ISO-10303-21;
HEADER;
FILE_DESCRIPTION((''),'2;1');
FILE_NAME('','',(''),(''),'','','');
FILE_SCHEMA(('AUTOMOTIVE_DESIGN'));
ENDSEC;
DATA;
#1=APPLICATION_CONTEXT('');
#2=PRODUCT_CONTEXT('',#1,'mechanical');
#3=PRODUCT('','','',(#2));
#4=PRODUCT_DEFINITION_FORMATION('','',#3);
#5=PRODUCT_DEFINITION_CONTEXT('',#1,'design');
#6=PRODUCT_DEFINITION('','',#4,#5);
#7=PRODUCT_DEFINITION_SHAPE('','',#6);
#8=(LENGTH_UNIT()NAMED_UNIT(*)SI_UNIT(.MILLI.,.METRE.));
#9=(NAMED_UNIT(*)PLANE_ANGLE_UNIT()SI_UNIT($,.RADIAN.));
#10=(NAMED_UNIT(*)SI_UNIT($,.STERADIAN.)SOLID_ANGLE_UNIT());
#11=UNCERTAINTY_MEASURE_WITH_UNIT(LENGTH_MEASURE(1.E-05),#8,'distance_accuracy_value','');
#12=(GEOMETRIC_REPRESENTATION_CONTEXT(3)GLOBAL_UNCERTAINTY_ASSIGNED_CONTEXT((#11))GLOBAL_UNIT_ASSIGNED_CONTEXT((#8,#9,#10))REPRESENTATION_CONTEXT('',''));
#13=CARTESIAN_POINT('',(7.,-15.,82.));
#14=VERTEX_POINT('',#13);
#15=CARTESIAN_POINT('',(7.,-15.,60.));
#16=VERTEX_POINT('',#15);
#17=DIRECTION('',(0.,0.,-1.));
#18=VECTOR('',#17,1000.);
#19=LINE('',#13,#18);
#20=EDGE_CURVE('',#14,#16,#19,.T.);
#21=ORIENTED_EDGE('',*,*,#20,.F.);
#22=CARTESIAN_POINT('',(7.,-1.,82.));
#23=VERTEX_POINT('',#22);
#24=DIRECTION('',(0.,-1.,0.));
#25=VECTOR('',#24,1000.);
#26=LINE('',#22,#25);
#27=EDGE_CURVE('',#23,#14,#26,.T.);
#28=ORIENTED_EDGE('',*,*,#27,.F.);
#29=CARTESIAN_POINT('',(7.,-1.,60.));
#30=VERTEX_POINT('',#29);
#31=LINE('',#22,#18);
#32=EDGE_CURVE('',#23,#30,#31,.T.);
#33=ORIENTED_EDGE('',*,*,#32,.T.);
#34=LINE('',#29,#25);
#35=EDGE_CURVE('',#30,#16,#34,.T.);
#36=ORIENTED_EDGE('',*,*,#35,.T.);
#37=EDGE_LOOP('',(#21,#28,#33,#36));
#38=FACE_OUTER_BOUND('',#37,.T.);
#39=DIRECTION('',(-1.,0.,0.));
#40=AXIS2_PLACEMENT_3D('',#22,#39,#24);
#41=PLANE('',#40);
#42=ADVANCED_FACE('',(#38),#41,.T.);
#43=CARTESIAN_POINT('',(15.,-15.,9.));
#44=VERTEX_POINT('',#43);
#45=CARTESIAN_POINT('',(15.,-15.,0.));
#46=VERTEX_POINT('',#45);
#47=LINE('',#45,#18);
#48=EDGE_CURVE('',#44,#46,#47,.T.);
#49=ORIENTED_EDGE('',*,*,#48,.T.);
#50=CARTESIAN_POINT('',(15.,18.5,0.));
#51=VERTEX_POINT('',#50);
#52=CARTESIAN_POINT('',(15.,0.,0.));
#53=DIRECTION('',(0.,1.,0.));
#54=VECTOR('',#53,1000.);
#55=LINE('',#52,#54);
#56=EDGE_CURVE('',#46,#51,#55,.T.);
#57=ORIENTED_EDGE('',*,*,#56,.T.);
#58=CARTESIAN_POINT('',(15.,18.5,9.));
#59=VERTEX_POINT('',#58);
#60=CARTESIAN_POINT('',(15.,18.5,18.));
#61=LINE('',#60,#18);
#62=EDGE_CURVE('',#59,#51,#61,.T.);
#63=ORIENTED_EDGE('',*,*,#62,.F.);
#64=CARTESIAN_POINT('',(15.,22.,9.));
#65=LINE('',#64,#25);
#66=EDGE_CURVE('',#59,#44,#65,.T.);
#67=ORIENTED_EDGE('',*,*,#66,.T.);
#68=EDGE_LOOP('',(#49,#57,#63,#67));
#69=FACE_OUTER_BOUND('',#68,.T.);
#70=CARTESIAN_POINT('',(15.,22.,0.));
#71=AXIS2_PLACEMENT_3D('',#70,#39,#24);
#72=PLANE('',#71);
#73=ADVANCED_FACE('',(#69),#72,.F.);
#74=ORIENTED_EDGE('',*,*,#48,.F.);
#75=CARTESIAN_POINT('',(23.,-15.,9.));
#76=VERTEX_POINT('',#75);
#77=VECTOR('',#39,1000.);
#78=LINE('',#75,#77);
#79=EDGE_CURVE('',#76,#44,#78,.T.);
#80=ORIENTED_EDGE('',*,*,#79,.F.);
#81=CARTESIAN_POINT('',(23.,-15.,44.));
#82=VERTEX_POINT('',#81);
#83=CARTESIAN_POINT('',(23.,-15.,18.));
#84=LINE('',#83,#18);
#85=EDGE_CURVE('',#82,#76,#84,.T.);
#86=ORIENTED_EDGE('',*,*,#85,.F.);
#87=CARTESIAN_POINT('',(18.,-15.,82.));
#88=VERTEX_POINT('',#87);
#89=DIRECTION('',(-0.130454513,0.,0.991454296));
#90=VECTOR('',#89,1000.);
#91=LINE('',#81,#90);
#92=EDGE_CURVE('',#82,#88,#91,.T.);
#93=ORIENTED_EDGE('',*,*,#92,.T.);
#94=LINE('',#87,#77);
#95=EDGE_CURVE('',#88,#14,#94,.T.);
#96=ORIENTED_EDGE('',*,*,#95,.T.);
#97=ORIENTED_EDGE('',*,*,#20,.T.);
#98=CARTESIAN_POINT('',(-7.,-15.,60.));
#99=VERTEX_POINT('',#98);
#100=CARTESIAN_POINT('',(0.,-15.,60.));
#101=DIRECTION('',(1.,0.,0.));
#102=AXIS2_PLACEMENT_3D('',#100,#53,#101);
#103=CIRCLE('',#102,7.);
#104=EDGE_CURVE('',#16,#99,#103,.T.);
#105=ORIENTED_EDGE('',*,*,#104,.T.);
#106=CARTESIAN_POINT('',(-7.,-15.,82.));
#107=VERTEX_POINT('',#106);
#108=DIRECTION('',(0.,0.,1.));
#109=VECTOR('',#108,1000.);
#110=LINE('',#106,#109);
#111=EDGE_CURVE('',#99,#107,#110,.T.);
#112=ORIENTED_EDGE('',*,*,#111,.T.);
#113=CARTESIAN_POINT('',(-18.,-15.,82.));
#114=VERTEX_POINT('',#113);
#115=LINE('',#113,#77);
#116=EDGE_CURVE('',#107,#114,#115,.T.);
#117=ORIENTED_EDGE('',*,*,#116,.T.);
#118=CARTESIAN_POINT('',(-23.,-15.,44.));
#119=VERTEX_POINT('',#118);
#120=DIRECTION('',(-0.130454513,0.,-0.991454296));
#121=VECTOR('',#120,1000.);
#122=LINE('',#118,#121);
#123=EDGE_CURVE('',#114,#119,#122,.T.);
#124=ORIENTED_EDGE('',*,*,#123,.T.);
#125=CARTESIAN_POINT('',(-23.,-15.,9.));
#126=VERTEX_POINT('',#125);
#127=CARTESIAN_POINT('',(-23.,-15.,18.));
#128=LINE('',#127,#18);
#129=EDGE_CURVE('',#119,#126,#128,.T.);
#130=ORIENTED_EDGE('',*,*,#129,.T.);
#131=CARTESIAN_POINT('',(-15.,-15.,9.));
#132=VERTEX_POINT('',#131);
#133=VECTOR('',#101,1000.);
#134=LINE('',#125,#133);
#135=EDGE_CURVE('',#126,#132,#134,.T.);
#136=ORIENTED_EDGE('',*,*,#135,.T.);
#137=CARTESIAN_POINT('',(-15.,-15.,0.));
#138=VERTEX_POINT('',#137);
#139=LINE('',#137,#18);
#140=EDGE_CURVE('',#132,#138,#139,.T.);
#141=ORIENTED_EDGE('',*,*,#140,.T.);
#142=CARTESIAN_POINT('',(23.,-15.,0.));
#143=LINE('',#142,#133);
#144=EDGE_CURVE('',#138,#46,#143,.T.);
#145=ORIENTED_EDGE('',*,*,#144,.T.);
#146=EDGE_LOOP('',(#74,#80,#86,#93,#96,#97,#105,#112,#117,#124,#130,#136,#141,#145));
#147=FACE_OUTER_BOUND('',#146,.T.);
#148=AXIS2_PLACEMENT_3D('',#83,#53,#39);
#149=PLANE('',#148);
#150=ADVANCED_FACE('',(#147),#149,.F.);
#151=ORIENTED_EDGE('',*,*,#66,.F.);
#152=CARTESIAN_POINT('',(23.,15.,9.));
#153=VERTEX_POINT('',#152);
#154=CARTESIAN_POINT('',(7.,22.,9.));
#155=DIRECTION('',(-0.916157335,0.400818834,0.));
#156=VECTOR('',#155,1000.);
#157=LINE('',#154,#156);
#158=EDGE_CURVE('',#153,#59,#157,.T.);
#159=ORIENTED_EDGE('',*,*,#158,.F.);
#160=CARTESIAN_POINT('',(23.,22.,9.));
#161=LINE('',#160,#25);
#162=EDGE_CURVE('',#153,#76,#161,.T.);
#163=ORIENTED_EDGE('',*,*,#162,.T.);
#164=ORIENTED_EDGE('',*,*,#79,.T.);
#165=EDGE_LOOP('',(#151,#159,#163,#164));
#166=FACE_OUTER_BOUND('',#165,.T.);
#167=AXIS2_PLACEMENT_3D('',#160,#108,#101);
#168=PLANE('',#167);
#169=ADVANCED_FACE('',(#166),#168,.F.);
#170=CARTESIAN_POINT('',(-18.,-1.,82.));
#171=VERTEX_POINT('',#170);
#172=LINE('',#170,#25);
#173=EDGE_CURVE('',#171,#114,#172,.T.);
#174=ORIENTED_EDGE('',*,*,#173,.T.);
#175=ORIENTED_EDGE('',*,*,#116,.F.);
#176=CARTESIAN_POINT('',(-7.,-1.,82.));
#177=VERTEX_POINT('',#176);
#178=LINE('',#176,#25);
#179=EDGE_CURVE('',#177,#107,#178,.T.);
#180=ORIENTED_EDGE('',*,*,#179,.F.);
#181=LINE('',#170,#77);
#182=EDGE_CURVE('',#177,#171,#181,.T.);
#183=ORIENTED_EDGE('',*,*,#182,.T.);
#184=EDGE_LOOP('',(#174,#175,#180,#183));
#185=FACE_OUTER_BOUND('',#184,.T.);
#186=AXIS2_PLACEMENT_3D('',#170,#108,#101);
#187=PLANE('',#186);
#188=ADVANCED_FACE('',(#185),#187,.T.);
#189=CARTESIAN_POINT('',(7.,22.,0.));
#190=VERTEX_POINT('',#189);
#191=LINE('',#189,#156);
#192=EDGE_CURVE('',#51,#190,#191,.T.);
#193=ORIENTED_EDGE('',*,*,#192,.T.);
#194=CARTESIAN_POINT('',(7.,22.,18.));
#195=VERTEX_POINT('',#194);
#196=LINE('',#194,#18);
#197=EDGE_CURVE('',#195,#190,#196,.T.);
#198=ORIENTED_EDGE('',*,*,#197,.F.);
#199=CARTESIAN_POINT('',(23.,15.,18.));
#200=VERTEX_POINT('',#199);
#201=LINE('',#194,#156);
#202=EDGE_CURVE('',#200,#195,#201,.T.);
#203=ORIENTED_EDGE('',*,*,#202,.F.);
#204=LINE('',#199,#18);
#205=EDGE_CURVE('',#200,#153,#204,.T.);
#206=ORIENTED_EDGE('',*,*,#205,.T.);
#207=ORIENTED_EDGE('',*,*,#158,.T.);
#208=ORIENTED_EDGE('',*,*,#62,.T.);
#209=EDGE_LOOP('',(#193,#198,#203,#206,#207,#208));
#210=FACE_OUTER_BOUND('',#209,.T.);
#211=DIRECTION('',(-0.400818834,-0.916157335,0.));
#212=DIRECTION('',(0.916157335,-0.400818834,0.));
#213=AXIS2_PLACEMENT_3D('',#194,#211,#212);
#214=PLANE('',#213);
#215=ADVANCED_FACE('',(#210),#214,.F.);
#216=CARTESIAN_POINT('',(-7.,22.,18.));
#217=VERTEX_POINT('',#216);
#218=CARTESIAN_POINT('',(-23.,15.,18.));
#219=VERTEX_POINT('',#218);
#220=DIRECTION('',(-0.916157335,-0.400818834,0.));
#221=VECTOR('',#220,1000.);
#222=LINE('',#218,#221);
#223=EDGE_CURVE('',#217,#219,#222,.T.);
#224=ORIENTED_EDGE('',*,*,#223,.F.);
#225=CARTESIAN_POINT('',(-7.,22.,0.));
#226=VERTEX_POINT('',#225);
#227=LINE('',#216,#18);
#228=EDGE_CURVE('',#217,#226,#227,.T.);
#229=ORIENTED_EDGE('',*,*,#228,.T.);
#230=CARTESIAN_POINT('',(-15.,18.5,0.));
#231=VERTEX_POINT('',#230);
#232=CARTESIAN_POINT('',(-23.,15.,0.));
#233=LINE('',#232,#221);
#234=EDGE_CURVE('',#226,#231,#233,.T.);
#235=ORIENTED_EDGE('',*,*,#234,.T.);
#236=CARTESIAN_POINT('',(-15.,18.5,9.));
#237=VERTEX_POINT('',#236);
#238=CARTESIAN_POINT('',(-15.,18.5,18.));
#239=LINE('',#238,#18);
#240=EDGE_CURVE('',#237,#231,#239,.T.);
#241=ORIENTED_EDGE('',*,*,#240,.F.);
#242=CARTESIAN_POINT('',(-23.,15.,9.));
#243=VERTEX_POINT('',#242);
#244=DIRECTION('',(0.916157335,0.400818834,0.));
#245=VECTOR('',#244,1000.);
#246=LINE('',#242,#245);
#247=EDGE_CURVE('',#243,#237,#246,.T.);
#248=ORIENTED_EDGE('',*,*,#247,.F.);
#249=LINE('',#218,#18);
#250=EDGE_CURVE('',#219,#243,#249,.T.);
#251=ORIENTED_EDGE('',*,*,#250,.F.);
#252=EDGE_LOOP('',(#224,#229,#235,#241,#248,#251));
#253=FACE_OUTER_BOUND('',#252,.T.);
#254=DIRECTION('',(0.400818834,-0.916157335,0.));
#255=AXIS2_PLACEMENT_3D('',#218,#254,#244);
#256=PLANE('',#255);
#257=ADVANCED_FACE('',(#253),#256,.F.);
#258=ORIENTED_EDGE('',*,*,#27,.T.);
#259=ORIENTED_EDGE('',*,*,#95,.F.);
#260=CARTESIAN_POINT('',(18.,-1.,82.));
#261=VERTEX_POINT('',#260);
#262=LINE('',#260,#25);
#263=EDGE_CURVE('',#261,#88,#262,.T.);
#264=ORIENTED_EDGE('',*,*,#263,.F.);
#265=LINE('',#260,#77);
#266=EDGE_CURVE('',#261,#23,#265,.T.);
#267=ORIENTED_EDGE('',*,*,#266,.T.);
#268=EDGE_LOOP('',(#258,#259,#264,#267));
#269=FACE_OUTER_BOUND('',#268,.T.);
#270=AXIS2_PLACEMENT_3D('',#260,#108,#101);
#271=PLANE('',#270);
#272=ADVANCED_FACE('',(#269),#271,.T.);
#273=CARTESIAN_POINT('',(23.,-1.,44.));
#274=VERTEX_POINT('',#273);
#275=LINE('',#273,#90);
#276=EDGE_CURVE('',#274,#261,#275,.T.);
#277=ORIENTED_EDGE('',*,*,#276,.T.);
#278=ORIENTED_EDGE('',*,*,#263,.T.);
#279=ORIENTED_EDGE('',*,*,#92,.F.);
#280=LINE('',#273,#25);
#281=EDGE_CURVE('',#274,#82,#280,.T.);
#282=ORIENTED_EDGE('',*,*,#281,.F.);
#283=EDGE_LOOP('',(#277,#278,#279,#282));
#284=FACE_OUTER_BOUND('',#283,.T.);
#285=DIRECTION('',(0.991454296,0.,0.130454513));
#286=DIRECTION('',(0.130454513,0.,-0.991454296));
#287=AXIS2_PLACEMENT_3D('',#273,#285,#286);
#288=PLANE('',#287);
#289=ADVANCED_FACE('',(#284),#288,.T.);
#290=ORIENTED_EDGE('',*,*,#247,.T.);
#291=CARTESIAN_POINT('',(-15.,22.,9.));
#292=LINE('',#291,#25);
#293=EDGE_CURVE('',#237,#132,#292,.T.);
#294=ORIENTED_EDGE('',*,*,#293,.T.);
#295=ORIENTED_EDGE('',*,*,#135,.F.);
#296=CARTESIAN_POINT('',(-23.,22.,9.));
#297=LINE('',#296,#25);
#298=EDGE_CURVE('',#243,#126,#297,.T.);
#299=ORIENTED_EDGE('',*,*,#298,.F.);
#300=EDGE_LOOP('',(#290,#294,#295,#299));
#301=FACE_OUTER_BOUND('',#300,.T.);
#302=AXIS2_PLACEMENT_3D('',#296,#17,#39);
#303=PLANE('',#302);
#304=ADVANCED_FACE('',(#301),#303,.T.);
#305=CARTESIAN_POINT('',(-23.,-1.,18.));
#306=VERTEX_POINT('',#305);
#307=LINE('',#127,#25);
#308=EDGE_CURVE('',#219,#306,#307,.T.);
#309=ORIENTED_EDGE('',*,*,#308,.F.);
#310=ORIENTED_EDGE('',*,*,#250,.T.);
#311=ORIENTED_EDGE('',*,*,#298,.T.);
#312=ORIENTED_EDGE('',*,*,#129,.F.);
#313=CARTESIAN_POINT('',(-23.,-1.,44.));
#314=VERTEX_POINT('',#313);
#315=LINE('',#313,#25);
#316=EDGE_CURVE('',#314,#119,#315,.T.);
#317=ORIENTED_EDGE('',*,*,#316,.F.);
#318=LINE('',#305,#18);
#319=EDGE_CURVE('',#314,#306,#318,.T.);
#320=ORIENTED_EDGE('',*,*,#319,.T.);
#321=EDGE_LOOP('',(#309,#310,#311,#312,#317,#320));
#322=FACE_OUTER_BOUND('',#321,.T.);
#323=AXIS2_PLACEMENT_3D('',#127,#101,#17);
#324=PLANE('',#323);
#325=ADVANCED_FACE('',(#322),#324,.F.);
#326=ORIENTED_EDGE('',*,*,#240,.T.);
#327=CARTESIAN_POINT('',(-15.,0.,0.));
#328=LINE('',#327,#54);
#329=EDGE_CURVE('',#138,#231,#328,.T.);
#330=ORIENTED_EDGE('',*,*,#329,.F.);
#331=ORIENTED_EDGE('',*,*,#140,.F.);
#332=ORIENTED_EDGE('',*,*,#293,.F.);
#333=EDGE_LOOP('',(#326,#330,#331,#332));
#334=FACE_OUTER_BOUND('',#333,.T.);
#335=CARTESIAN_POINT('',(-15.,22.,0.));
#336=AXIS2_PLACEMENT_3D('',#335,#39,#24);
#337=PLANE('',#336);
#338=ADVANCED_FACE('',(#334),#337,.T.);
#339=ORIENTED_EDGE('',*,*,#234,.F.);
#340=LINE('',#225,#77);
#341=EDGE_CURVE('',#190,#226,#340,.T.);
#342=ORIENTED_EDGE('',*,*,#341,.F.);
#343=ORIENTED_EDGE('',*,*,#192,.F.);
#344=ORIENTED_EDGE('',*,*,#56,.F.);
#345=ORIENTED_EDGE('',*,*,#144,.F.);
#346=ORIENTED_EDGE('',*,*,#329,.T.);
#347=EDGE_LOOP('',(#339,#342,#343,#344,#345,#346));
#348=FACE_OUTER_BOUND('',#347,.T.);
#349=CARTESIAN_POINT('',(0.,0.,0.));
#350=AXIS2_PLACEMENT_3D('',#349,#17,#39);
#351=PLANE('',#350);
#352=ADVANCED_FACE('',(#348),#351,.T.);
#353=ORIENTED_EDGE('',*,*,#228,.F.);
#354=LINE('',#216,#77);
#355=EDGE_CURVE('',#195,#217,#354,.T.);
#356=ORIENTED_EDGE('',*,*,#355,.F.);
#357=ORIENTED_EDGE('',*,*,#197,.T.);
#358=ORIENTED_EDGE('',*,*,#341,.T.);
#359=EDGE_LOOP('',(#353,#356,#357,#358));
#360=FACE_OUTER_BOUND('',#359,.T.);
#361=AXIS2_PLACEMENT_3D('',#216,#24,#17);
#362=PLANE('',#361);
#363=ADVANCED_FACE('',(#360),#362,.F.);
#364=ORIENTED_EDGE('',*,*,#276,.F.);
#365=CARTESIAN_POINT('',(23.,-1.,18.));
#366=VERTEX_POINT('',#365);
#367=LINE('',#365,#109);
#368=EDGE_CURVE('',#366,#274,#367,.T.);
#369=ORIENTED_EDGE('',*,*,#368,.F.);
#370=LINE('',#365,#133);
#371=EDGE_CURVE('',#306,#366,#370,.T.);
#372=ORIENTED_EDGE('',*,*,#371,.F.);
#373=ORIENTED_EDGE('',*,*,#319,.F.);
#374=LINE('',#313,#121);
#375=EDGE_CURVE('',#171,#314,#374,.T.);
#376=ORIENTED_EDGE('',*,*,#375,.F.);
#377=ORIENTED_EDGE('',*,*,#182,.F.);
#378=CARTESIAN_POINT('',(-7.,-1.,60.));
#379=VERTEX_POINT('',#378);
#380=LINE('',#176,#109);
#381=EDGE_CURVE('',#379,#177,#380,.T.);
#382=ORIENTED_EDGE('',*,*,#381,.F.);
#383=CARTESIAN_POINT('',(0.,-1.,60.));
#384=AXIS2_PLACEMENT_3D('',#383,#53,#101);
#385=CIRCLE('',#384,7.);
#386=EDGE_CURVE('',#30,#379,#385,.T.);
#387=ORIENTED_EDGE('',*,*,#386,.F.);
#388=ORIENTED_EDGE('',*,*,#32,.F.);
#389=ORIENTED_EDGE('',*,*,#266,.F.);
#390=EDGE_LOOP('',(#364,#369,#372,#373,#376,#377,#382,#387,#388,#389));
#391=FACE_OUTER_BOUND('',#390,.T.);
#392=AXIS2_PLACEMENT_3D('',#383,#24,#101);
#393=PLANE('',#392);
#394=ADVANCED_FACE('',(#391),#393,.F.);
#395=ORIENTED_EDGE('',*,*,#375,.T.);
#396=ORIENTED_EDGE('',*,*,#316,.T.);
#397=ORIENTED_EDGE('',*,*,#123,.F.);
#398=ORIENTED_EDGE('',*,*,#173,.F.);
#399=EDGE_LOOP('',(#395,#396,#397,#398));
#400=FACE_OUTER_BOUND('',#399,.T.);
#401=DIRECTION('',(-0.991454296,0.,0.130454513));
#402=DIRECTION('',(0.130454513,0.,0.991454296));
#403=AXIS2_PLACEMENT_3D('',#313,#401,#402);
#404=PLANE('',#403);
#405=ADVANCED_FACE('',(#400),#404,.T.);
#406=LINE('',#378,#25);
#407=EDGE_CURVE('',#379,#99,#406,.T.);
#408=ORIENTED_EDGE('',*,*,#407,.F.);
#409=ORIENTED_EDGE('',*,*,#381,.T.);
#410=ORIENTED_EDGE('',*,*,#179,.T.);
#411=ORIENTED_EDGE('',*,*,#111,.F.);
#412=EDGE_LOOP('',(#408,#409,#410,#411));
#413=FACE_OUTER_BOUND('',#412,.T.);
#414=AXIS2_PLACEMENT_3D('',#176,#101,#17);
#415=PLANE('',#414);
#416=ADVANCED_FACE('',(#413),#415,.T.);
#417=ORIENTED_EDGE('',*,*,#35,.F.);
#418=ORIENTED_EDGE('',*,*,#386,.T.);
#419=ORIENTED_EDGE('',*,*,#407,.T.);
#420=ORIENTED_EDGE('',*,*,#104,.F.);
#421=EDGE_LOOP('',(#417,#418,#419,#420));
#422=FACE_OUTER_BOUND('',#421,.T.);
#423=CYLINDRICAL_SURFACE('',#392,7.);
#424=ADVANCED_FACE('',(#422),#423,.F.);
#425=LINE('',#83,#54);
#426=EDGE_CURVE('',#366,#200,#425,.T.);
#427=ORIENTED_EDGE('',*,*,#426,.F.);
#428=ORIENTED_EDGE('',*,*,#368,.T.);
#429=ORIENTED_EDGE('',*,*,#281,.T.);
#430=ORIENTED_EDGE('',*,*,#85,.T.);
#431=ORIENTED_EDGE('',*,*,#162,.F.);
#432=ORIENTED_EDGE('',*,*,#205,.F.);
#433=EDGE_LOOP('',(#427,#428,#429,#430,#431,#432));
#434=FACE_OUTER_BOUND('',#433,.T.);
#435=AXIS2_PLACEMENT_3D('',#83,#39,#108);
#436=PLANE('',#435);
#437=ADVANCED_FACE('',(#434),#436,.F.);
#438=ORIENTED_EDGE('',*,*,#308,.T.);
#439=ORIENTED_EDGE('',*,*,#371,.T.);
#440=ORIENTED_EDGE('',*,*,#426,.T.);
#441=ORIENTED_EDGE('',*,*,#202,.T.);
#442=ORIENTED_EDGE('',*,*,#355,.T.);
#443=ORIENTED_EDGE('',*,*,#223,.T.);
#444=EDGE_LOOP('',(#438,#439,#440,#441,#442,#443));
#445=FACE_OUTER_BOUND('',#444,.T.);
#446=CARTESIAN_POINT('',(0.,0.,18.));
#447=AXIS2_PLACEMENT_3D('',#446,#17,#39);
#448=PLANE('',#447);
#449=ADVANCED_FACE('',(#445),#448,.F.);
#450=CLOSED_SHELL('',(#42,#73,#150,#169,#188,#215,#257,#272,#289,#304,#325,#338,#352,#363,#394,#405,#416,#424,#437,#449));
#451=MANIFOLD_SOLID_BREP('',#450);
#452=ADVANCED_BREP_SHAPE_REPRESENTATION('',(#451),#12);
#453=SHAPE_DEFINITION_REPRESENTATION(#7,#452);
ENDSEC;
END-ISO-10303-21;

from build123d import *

# Parameters (mm, degrees)
FORKED_BASE_DEPTH   = 18
UPRIGHT_BOSS_DEPTH  = 14
NOTCH_SKETCH_8X9_W  = 8
NOTCH_SKETCH_8X9_H  = 9
NOTCH_CUT_8X9_DEPTH = 93.854725243


with BuildPart() as part:
    # Base Profile Sketch → Forked Base (new body)
    with BuildSketch(Plane.XY):
        Polygon((-23, 15), (-7, 22), (7, 22), (23, 15), (23, -15), (-23, -15), align=None)
    extrude(amount=FORKED_BASE_DEPTH)

    # Upright Profile Sketch → Upright Boss (add)
    with BuildSketch(Plane(origin=(0, -15, 0), x_dir=(-1, 0, 0), z_dir=(0, -1, 0))):
        with BuildLine():
            Line((-23, -18), (-23, -44))
            Line((-23, -44), (-18, -82))
            Line((-18, -82), (-7, -82))
            Line((-7, -82), (-7, -60))
            ThreePointArc((-7, -60), (0, -53), (7, -60))
            Line((7, -60), (7, -82))
            Line((7, -82), (18, -82))
            Line((18, -82), (23, -44))
            Line((23, -44), (23, -18))
            Line((23, -18), (-23, -18))
        make_face()
    extrude(amount=-UPRIGHT_BOSS_DEPTH)

    # Notch Sketch 8x9 → Notch Cut 8x9 (cut, through all)
    with BuildSketch(Plane.XZ.offset(15)):
        with Locations((19, 4.5)):
            Rectangle(NOTCH_SKETCH_8X9_W, NOTCH_SKETCH_8X9_H)
    notch_cut_8x9 = extrude(amount=-NOTCH_CUT_8X9_DEPTH, mode=Mode.SUBTRACT)

    # Notch Mirror: Notch Cut 8x9 across plane
    add(notch_cut_8x9.mirror(Plane(origin=(0, 0, 0), x_dir=(0, 0, 1), z_dir=(1, 0, 0))), mode=Mode.SUBTRACT)


solid = part.part
